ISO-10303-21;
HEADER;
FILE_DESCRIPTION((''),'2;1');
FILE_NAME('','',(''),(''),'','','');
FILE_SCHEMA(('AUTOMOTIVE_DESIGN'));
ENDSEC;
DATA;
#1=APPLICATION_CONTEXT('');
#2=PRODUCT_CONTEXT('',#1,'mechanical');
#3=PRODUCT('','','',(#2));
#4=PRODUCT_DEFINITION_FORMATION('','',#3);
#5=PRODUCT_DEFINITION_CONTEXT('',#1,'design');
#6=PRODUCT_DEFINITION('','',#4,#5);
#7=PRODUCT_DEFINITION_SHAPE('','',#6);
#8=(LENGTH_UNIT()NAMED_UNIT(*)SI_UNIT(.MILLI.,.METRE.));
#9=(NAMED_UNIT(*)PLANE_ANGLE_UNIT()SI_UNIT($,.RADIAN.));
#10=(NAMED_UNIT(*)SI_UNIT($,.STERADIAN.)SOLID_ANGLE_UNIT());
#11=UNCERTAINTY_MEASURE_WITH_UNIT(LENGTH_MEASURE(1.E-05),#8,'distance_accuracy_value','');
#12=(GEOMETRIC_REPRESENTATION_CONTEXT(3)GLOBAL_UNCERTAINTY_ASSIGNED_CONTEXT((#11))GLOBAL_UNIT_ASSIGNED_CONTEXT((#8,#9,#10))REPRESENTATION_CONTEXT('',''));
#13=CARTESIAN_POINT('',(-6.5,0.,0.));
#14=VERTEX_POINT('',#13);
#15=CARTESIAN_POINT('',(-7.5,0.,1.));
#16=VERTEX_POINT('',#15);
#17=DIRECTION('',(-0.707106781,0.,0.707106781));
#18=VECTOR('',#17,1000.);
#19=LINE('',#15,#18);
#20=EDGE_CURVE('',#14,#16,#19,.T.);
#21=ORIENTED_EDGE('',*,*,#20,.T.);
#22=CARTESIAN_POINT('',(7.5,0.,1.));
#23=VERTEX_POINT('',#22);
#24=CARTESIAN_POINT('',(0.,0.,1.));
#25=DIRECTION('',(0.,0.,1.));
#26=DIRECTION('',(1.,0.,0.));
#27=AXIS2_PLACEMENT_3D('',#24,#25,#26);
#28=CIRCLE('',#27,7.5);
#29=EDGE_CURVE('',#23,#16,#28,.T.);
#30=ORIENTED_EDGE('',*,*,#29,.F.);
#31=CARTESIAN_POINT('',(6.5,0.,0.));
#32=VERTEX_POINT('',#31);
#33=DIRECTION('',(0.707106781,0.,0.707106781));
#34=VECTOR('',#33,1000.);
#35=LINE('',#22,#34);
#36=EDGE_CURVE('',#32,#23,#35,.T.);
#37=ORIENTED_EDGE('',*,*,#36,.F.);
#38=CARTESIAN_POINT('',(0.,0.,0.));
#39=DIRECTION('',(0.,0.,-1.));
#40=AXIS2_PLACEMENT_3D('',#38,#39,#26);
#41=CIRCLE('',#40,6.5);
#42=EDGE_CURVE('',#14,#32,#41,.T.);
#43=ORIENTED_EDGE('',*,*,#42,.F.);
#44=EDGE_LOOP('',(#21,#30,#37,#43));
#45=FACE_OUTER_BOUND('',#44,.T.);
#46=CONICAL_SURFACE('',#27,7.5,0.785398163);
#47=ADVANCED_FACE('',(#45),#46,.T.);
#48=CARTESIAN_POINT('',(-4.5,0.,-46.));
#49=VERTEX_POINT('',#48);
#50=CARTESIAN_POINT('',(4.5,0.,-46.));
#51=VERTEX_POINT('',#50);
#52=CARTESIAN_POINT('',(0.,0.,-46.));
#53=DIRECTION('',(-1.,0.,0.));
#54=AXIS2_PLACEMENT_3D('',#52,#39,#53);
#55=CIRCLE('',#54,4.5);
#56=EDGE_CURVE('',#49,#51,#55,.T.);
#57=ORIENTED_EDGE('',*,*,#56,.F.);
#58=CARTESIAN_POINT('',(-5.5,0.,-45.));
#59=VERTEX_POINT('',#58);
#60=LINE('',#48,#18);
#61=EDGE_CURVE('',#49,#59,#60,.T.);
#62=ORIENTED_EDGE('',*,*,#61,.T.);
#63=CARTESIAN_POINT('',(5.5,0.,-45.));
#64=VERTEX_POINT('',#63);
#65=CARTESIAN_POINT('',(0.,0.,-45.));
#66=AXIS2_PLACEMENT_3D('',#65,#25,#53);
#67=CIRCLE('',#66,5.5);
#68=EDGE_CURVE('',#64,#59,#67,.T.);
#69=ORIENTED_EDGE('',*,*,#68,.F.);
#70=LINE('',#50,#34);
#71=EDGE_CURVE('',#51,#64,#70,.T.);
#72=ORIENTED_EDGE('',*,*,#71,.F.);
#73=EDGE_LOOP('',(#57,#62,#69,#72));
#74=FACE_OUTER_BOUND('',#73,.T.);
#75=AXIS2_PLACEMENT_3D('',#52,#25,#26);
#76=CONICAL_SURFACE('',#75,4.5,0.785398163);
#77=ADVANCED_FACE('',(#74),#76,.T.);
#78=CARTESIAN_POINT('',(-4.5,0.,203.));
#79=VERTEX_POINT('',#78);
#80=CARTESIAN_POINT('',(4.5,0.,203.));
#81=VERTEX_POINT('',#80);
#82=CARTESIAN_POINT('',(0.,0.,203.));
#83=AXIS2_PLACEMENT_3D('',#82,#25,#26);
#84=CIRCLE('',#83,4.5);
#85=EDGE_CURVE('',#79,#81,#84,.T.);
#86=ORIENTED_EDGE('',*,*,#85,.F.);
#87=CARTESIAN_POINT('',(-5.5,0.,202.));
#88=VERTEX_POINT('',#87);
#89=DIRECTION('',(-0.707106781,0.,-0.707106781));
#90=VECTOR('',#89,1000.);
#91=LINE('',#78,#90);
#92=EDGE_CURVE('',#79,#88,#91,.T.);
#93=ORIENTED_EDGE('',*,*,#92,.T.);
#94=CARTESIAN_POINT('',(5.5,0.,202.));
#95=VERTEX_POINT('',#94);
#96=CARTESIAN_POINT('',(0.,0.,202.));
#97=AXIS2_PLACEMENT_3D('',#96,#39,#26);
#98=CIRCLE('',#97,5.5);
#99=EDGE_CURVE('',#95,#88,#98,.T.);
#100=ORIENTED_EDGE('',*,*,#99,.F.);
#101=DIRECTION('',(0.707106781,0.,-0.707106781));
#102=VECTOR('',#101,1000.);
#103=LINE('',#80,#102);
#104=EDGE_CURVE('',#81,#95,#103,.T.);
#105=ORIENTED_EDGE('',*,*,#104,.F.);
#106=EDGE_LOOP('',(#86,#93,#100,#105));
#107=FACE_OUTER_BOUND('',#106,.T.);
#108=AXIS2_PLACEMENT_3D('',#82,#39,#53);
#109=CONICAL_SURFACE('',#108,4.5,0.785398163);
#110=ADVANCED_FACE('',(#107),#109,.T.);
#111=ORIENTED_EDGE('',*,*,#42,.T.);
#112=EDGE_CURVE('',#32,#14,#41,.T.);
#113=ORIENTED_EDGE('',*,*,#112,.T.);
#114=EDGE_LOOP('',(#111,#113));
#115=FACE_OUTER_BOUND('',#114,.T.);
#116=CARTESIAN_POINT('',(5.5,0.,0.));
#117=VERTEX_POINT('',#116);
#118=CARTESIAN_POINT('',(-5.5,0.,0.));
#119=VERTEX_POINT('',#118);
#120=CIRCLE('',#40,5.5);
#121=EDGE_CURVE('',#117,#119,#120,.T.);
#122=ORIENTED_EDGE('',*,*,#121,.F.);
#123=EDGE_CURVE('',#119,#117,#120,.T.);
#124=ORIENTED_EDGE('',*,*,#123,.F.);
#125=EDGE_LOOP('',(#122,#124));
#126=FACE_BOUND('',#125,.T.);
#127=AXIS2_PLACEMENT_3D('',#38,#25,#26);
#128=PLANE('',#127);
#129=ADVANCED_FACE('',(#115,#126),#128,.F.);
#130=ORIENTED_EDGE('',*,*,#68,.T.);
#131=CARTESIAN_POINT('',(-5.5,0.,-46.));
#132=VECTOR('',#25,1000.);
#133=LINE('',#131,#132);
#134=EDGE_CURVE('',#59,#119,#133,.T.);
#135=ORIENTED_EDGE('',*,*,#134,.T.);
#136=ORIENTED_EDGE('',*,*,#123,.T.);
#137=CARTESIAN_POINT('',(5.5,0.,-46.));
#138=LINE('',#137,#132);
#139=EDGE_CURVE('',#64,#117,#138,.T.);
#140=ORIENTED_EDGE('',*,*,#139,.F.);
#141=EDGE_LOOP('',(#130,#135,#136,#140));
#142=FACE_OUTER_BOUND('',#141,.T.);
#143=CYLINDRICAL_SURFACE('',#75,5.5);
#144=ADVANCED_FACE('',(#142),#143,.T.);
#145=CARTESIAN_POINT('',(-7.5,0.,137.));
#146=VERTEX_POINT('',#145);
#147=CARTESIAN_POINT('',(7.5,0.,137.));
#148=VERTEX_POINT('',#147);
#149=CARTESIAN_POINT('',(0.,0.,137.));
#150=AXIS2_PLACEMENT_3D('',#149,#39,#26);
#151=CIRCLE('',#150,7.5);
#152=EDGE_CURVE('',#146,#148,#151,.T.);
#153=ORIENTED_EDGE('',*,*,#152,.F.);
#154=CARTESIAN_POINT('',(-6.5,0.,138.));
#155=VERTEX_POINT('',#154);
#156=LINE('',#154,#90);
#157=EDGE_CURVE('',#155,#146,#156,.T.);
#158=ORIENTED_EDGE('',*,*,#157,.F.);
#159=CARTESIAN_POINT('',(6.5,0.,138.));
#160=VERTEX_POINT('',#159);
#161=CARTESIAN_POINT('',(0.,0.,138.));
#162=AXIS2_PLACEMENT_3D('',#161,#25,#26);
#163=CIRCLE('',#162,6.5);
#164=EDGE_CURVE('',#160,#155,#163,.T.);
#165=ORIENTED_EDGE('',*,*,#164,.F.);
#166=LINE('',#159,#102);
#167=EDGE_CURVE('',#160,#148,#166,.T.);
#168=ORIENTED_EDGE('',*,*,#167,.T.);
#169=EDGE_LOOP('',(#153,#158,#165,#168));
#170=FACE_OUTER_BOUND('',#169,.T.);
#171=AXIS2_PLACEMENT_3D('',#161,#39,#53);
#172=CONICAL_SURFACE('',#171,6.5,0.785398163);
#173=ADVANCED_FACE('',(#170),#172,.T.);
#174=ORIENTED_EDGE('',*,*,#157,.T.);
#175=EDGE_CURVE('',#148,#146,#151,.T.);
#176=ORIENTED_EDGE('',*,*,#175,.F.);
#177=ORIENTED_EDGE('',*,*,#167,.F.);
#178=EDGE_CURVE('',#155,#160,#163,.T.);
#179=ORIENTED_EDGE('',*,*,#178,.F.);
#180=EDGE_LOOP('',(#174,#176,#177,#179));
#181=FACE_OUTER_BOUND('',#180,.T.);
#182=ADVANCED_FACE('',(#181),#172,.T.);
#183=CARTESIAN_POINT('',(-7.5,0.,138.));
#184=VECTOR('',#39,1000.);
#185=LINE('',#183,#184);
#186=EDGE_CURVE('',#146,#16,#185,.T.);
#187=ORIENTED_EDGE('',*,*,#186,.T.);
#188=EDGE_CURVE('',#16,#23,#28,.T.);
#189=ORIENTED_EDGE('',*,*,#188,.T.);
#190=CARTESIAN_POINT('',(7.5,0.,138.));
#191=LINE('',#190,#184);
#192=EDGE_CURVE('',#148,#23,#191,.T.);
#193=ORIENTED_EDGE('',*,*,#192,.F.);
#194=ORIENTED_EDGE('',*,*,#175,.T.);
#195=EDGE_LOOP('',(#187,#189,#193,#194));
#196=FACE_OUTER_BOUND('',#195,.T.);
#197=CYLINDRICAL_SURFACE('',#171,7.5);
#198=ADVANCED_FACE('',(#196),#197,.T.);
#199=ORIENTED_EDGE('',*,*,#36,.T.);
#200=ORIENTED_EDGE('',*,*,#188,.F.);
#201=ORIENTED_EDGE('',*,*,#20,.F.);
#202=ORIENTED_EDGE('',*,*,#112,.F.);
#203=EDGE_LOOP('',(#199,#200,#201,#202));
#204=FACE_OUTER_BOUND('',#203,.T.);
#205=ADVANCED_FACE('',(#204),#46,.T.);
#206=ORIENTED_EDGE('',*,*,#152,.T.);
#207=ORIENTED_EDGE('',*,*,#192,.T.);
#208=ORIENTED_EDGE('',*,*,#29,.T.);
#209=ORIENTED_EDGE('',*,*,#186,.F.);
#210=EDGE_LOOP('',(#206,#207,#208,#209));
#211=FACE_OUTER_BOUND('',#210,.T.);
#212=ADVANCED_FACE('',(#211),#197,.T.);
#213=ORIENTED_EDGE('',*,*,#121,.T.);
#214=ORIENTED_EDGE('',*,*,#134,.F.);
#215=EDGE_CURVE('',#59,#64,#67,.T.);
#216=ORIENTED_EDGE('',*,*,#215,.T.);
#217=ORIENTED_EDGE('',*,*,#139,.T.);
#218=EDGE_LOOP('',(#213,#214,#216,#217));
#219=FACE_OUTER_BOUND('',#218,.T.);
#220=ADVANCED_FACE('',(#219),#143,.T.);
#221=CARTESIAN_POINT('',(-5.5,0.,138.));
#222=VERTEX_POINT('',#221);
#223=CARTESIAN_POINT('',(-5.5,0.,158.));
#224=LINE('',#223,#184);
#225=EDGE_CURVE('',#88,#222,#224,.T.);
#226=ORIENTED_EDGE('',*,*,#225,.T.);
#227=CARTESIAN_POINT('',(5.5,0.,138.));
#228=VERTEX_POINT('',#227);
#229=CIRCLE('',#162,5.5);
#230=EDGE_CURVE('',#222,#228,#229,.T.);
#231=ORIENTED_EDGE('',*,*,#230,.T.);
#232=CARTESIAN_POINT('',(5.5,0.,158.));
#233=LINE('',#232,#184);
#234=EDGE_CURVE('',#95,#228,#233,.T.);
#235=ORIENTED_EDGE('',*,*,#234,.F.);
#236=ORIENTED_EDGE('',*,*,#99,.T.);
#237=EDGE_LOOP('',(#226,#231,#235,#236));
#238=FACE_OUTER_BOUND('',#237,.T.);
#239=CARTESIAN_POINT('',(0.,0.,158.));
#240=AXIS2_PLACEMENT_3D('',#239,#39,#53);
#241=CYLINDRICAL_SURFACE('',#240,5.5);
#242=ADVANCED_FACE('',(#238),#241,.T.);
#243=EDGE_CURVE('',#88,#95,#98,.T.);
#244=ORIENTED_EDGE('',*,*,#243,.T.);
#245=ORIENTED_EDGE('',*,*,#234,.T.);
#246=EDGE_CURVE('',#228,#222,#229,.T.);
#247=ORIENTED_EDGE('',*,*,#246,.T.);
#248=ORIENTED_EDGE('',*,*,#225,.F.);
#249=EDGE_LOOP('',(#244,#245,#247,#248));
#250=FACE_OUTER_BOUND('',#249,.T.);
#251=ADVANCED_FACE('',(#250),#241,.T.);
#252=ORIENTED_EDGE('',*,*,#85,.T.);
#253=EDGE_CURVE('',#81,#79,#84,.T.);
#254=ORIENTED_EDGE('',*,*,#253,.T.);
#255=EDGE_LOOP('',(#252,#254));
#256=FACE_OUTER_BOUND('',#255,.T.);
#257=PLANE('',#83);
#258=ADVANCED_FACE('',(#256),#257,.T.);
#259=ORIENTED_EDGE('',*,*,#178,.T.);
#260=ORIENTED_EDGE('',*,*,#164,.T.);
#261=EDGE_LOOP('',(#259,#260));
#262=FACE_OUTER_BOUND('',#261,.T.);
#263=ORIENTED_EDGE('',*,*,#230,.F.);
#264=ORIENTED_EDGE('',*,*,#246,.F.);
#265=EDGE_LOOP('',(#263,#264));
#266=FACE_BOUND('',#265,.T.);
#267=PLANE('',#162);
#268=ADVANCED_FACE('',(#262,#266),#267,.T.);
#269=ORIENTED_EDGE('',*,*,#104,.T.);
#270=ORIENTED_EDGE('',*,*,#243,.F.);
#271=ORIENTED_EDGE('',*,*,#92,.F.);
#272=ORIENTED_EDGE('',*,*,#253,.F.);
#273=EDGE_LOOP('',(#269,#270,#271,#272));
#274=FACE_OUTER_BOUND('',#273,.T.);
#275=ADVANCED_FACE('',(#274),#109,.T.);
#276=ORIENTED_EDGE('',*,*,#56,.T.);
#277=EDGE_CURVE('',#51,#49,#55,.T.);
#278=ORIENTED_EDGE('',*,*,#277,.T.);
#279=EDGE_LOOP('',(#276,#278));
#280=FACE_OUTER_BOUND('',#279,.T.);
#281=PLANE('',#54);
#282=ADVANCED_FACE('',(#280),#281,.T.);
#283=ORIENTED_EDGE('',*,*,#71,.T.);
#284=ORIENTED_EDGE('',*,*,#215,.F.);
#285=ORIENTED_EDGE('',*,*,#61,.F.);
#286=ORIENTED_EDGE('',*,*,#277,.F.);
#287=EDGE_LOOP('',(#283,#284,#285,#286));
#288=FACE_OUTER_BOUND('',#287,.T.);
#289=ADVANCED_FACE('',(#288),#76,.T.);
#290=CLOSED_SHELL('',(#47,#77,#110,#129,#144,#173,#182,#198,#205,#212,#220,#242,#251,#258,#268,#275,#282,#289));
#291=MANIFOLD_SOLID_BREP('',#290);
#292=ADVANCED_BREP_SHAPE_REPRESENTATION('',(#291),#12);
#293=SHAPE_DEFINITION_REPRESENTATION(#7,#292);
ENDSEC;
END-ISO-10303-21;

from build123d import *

# Parameters (mm, degrees)
SKETCH1_R           = 7.5
BOSS_EXTRUDE1_DEPTH = 138
SKETCH2_R           = 5.5
BOSS_EXTRUDE2_DEPTH = 20
SKETCH3_R           = 5.5
BOSS_EXTRUDE3_DEPTH = 45
CHAMFER1_SIZE       = 1
BOSS_EXTRUDE4_START = 46
SKETCH4_R           = 5.5
BOSS_EXTRUDE4_DEPTH = 46
CHAMFER2_SIZE       = 1


with BuildPart() as part:
    # Sketch1 → Boss-Extrude1 (new body)
    with BuildSketch(Plane.XY):
        Circle(SKETCH1_R)
    extrude(amount=BOSS_EXTRUDE1_DEPTH)

    # Sketch2 → Boss-Extrude2 (add)
    with BuildSketch(Plane.XY.offset(138)):
        Circle(SKETCH2_R)
    extrude(amount=BOSS_EXTRUDE2_DEPTH)

    # Sketch3 → Boss-Extrude3 (add)
    with BuildSketch(Plane.XY.offset(158)):
        Circle(SKETCH3_R)
    extrude(amount=BOSS_EXTRUDE3_DEPTH)

    # Chamfer1
    chamfer1_edges = [part.edges().sort_by_distance(p)[0] for p in [
        (-7.5, 0, 0),
        (-7.5, 0, 138),
        (-5.5, 0, 203),
    ]]
    chamfer(chamfer1_edges, length=CHAMFER1_SIZE)

    # Sketch4 → Boss-Extrude4 (add)
    with BuildSketch(Plane(origin=(0, 0, 0), x_dir=(-1, 0, 0), z_dir=(0, 0, -1)).offset(BOSS_EXTRUDE4_START)):
        with Locations(Location((0, 0, 0), (0, 0, 180))):
            Circle(SKETCH4_R)
    extrude(amount=-BOSS_EXTRUDE4_DEPTH)

    # Chamfer2
    chamfer2_edges = [part.edges().sort_by_distance(p)[0] for p in [
        (-5.5, 0, -46),
    ]]
    chamfer(chamfer2_edges, length=CHAMFER2_SIZE)


solid = part.part
